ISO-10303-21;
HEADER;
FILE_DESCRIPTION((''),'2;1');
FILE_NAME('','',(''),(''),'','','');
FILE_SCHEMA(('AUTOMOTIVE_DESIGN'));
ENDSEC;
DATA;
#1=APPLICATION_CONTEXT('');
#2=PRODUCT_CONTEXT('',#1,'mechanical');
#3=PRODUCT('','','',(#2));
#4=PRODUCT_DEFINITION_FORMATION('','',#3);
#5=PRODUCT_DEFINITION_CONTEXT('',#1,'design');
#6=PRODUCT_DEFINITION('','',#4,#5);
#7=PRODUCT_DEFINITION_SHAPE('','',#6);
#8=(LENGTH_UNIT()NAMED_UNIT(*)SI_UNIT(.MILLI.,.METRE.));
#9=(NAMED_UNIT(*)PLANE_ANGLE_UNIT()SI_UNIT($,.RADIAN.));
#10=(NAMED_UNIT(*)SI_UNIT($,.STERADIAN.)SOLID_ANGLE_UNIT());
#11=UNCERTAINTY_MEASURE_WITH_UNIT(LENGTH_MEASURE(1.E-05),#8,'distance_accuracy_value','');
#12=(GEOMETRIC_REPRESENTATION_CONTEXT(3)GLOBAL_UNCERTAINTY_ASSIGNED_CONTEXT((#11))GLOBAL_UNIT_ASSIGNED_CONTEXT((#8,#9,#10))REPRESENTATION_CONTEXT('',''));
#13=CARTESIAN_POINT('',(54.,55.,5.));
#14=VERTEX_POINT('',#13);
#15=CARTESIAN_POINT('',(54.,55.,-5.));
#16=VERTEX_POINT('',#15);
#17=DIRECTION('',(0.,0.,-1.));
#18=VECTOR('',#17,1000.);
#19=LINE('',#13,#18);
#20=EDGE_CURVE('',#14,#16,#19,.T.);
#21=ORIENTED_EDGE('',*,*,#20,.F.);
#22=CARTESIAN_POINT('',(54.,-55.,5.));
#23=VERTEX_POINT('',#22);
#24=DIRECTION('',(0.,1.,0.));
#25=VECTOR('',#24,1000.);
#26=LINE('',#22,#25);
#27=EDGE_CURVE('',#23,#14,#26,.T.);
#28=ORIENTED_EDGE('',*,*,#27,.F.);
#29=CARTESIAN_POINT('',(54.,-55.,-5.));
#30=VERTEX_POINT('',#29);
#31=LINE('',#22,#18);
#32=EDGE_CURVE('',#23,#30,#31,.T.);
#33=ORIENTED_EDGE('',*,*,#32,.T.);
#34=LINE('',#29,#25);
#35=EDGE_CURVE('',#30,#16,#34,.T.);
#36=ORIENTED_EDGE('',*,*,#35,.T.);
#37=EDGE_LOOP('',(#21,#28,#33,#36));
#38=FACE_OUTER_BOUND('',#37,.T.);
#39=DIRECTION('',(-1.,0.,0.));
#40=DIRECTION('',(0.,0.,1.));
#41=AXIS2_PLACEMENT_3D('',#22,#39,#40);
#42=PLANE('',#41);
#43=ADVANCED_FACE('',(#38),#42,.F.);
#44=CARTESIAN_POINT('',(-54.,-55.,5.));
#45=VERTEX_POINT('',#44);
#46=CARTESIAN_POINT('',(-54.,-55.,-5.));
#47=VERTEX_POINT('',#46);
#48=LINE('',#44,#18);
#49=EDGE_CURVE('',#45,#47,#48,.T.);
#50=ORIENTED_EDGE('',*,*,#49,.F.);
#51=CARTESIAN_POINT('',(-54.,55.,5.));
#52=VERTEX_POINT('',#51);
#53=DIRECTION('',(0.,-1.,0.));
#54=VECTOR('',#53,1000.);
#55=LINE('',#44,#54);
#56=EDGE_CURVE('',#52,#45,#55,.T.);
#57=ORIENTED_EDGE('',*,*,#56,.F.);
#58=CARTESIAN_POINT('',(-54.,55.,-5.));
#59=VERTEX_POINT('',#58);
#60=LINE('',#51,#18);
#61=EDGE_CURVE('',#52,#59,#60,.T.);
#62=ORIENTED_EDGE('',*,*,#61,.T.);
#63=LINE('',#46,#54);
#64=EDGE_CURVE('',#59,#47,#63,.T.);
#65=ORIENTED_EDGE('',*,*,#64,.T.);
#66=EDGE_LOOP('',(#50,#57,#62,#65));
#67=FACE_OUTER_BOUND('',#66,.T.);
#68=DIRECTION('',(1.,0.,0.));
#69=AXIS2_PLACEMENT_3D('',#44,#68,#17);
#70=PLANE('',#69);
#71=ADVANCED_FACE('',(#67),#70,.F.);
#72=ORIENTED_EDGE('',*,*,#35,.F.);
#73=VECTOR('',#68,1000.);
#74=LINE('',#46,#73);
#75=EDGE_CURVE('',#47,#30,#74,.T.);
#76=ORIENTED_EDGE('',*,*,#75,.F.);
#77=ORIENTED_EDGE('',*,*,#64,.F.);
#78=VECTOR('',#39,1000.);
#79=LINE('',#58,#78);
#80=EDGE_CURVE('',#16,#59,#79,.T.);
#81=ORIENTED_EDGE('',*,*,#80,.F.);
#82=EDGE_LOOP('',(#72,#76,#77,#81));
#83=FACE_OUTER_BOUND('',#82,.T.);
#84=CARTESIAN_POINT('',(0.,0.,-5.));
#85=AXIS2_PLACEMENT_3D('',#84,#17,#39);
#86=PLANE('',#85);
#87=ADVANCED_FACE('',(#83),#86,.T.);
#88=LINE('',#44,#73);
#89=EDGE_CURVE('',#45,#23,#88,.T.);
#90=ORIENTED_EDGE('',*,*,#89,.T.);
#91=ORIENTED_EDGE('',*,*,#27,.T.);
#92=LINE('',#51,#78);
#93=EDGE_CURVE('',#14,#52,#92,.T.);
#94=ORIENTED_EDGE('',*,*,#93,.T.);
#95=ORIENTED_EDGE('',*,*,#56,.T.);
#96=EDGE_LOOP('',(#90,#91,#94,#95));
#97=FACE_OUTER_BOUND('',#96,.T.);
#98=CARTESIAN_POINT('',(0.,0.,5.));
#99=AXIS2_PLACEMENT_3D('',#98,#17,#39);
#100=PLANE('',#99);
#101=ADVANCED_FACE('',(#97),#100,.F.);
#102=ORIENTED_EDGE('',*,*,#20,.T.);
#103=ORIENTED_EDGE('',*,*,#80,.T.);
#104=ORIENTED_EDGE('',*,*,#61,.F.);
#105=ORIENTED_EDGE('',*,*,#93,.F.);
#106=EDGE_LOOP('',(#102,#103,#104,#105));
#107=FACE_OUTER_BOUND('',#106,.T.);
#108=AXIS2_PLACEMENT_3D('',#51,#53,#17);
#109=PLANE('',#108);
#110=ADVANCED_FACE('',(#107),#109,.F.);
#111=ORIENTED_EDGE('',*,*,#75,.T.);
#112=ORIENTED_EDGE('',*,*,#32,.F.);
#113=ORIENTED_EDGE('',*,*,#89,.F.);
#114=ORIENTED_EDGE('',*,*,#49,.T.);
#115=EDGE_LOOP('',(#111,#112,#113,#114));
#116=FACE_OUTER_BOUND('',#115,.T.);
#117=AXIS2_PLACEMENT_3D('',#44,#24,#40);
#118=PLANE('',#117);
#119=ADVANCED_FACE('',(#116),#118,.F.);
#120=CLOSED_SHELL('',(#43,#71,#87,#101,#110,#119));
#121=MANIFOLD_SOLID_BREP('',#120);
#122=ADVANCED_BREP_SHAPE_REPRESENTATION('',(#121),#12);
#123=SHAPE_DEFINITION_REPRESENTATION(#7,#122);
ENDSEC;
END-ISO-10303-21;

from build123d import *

# Parameters (mm, degrees)
SKETCH_1_W      = 108
SKETCH_1_H      = 110
EXTRUDE_1_DEPTH = 5


with BuildPart() as part:
    # 草图1 → 凸台-拉伸1 (new, symmetric)
    with BuildSketch(Plane.XY):
        Rectangle(SKETCH_1_W, SKETCH_1_H)
    extrude(amount=EXTRUDE_1_DEPTH, both=True)


solid = part.part
